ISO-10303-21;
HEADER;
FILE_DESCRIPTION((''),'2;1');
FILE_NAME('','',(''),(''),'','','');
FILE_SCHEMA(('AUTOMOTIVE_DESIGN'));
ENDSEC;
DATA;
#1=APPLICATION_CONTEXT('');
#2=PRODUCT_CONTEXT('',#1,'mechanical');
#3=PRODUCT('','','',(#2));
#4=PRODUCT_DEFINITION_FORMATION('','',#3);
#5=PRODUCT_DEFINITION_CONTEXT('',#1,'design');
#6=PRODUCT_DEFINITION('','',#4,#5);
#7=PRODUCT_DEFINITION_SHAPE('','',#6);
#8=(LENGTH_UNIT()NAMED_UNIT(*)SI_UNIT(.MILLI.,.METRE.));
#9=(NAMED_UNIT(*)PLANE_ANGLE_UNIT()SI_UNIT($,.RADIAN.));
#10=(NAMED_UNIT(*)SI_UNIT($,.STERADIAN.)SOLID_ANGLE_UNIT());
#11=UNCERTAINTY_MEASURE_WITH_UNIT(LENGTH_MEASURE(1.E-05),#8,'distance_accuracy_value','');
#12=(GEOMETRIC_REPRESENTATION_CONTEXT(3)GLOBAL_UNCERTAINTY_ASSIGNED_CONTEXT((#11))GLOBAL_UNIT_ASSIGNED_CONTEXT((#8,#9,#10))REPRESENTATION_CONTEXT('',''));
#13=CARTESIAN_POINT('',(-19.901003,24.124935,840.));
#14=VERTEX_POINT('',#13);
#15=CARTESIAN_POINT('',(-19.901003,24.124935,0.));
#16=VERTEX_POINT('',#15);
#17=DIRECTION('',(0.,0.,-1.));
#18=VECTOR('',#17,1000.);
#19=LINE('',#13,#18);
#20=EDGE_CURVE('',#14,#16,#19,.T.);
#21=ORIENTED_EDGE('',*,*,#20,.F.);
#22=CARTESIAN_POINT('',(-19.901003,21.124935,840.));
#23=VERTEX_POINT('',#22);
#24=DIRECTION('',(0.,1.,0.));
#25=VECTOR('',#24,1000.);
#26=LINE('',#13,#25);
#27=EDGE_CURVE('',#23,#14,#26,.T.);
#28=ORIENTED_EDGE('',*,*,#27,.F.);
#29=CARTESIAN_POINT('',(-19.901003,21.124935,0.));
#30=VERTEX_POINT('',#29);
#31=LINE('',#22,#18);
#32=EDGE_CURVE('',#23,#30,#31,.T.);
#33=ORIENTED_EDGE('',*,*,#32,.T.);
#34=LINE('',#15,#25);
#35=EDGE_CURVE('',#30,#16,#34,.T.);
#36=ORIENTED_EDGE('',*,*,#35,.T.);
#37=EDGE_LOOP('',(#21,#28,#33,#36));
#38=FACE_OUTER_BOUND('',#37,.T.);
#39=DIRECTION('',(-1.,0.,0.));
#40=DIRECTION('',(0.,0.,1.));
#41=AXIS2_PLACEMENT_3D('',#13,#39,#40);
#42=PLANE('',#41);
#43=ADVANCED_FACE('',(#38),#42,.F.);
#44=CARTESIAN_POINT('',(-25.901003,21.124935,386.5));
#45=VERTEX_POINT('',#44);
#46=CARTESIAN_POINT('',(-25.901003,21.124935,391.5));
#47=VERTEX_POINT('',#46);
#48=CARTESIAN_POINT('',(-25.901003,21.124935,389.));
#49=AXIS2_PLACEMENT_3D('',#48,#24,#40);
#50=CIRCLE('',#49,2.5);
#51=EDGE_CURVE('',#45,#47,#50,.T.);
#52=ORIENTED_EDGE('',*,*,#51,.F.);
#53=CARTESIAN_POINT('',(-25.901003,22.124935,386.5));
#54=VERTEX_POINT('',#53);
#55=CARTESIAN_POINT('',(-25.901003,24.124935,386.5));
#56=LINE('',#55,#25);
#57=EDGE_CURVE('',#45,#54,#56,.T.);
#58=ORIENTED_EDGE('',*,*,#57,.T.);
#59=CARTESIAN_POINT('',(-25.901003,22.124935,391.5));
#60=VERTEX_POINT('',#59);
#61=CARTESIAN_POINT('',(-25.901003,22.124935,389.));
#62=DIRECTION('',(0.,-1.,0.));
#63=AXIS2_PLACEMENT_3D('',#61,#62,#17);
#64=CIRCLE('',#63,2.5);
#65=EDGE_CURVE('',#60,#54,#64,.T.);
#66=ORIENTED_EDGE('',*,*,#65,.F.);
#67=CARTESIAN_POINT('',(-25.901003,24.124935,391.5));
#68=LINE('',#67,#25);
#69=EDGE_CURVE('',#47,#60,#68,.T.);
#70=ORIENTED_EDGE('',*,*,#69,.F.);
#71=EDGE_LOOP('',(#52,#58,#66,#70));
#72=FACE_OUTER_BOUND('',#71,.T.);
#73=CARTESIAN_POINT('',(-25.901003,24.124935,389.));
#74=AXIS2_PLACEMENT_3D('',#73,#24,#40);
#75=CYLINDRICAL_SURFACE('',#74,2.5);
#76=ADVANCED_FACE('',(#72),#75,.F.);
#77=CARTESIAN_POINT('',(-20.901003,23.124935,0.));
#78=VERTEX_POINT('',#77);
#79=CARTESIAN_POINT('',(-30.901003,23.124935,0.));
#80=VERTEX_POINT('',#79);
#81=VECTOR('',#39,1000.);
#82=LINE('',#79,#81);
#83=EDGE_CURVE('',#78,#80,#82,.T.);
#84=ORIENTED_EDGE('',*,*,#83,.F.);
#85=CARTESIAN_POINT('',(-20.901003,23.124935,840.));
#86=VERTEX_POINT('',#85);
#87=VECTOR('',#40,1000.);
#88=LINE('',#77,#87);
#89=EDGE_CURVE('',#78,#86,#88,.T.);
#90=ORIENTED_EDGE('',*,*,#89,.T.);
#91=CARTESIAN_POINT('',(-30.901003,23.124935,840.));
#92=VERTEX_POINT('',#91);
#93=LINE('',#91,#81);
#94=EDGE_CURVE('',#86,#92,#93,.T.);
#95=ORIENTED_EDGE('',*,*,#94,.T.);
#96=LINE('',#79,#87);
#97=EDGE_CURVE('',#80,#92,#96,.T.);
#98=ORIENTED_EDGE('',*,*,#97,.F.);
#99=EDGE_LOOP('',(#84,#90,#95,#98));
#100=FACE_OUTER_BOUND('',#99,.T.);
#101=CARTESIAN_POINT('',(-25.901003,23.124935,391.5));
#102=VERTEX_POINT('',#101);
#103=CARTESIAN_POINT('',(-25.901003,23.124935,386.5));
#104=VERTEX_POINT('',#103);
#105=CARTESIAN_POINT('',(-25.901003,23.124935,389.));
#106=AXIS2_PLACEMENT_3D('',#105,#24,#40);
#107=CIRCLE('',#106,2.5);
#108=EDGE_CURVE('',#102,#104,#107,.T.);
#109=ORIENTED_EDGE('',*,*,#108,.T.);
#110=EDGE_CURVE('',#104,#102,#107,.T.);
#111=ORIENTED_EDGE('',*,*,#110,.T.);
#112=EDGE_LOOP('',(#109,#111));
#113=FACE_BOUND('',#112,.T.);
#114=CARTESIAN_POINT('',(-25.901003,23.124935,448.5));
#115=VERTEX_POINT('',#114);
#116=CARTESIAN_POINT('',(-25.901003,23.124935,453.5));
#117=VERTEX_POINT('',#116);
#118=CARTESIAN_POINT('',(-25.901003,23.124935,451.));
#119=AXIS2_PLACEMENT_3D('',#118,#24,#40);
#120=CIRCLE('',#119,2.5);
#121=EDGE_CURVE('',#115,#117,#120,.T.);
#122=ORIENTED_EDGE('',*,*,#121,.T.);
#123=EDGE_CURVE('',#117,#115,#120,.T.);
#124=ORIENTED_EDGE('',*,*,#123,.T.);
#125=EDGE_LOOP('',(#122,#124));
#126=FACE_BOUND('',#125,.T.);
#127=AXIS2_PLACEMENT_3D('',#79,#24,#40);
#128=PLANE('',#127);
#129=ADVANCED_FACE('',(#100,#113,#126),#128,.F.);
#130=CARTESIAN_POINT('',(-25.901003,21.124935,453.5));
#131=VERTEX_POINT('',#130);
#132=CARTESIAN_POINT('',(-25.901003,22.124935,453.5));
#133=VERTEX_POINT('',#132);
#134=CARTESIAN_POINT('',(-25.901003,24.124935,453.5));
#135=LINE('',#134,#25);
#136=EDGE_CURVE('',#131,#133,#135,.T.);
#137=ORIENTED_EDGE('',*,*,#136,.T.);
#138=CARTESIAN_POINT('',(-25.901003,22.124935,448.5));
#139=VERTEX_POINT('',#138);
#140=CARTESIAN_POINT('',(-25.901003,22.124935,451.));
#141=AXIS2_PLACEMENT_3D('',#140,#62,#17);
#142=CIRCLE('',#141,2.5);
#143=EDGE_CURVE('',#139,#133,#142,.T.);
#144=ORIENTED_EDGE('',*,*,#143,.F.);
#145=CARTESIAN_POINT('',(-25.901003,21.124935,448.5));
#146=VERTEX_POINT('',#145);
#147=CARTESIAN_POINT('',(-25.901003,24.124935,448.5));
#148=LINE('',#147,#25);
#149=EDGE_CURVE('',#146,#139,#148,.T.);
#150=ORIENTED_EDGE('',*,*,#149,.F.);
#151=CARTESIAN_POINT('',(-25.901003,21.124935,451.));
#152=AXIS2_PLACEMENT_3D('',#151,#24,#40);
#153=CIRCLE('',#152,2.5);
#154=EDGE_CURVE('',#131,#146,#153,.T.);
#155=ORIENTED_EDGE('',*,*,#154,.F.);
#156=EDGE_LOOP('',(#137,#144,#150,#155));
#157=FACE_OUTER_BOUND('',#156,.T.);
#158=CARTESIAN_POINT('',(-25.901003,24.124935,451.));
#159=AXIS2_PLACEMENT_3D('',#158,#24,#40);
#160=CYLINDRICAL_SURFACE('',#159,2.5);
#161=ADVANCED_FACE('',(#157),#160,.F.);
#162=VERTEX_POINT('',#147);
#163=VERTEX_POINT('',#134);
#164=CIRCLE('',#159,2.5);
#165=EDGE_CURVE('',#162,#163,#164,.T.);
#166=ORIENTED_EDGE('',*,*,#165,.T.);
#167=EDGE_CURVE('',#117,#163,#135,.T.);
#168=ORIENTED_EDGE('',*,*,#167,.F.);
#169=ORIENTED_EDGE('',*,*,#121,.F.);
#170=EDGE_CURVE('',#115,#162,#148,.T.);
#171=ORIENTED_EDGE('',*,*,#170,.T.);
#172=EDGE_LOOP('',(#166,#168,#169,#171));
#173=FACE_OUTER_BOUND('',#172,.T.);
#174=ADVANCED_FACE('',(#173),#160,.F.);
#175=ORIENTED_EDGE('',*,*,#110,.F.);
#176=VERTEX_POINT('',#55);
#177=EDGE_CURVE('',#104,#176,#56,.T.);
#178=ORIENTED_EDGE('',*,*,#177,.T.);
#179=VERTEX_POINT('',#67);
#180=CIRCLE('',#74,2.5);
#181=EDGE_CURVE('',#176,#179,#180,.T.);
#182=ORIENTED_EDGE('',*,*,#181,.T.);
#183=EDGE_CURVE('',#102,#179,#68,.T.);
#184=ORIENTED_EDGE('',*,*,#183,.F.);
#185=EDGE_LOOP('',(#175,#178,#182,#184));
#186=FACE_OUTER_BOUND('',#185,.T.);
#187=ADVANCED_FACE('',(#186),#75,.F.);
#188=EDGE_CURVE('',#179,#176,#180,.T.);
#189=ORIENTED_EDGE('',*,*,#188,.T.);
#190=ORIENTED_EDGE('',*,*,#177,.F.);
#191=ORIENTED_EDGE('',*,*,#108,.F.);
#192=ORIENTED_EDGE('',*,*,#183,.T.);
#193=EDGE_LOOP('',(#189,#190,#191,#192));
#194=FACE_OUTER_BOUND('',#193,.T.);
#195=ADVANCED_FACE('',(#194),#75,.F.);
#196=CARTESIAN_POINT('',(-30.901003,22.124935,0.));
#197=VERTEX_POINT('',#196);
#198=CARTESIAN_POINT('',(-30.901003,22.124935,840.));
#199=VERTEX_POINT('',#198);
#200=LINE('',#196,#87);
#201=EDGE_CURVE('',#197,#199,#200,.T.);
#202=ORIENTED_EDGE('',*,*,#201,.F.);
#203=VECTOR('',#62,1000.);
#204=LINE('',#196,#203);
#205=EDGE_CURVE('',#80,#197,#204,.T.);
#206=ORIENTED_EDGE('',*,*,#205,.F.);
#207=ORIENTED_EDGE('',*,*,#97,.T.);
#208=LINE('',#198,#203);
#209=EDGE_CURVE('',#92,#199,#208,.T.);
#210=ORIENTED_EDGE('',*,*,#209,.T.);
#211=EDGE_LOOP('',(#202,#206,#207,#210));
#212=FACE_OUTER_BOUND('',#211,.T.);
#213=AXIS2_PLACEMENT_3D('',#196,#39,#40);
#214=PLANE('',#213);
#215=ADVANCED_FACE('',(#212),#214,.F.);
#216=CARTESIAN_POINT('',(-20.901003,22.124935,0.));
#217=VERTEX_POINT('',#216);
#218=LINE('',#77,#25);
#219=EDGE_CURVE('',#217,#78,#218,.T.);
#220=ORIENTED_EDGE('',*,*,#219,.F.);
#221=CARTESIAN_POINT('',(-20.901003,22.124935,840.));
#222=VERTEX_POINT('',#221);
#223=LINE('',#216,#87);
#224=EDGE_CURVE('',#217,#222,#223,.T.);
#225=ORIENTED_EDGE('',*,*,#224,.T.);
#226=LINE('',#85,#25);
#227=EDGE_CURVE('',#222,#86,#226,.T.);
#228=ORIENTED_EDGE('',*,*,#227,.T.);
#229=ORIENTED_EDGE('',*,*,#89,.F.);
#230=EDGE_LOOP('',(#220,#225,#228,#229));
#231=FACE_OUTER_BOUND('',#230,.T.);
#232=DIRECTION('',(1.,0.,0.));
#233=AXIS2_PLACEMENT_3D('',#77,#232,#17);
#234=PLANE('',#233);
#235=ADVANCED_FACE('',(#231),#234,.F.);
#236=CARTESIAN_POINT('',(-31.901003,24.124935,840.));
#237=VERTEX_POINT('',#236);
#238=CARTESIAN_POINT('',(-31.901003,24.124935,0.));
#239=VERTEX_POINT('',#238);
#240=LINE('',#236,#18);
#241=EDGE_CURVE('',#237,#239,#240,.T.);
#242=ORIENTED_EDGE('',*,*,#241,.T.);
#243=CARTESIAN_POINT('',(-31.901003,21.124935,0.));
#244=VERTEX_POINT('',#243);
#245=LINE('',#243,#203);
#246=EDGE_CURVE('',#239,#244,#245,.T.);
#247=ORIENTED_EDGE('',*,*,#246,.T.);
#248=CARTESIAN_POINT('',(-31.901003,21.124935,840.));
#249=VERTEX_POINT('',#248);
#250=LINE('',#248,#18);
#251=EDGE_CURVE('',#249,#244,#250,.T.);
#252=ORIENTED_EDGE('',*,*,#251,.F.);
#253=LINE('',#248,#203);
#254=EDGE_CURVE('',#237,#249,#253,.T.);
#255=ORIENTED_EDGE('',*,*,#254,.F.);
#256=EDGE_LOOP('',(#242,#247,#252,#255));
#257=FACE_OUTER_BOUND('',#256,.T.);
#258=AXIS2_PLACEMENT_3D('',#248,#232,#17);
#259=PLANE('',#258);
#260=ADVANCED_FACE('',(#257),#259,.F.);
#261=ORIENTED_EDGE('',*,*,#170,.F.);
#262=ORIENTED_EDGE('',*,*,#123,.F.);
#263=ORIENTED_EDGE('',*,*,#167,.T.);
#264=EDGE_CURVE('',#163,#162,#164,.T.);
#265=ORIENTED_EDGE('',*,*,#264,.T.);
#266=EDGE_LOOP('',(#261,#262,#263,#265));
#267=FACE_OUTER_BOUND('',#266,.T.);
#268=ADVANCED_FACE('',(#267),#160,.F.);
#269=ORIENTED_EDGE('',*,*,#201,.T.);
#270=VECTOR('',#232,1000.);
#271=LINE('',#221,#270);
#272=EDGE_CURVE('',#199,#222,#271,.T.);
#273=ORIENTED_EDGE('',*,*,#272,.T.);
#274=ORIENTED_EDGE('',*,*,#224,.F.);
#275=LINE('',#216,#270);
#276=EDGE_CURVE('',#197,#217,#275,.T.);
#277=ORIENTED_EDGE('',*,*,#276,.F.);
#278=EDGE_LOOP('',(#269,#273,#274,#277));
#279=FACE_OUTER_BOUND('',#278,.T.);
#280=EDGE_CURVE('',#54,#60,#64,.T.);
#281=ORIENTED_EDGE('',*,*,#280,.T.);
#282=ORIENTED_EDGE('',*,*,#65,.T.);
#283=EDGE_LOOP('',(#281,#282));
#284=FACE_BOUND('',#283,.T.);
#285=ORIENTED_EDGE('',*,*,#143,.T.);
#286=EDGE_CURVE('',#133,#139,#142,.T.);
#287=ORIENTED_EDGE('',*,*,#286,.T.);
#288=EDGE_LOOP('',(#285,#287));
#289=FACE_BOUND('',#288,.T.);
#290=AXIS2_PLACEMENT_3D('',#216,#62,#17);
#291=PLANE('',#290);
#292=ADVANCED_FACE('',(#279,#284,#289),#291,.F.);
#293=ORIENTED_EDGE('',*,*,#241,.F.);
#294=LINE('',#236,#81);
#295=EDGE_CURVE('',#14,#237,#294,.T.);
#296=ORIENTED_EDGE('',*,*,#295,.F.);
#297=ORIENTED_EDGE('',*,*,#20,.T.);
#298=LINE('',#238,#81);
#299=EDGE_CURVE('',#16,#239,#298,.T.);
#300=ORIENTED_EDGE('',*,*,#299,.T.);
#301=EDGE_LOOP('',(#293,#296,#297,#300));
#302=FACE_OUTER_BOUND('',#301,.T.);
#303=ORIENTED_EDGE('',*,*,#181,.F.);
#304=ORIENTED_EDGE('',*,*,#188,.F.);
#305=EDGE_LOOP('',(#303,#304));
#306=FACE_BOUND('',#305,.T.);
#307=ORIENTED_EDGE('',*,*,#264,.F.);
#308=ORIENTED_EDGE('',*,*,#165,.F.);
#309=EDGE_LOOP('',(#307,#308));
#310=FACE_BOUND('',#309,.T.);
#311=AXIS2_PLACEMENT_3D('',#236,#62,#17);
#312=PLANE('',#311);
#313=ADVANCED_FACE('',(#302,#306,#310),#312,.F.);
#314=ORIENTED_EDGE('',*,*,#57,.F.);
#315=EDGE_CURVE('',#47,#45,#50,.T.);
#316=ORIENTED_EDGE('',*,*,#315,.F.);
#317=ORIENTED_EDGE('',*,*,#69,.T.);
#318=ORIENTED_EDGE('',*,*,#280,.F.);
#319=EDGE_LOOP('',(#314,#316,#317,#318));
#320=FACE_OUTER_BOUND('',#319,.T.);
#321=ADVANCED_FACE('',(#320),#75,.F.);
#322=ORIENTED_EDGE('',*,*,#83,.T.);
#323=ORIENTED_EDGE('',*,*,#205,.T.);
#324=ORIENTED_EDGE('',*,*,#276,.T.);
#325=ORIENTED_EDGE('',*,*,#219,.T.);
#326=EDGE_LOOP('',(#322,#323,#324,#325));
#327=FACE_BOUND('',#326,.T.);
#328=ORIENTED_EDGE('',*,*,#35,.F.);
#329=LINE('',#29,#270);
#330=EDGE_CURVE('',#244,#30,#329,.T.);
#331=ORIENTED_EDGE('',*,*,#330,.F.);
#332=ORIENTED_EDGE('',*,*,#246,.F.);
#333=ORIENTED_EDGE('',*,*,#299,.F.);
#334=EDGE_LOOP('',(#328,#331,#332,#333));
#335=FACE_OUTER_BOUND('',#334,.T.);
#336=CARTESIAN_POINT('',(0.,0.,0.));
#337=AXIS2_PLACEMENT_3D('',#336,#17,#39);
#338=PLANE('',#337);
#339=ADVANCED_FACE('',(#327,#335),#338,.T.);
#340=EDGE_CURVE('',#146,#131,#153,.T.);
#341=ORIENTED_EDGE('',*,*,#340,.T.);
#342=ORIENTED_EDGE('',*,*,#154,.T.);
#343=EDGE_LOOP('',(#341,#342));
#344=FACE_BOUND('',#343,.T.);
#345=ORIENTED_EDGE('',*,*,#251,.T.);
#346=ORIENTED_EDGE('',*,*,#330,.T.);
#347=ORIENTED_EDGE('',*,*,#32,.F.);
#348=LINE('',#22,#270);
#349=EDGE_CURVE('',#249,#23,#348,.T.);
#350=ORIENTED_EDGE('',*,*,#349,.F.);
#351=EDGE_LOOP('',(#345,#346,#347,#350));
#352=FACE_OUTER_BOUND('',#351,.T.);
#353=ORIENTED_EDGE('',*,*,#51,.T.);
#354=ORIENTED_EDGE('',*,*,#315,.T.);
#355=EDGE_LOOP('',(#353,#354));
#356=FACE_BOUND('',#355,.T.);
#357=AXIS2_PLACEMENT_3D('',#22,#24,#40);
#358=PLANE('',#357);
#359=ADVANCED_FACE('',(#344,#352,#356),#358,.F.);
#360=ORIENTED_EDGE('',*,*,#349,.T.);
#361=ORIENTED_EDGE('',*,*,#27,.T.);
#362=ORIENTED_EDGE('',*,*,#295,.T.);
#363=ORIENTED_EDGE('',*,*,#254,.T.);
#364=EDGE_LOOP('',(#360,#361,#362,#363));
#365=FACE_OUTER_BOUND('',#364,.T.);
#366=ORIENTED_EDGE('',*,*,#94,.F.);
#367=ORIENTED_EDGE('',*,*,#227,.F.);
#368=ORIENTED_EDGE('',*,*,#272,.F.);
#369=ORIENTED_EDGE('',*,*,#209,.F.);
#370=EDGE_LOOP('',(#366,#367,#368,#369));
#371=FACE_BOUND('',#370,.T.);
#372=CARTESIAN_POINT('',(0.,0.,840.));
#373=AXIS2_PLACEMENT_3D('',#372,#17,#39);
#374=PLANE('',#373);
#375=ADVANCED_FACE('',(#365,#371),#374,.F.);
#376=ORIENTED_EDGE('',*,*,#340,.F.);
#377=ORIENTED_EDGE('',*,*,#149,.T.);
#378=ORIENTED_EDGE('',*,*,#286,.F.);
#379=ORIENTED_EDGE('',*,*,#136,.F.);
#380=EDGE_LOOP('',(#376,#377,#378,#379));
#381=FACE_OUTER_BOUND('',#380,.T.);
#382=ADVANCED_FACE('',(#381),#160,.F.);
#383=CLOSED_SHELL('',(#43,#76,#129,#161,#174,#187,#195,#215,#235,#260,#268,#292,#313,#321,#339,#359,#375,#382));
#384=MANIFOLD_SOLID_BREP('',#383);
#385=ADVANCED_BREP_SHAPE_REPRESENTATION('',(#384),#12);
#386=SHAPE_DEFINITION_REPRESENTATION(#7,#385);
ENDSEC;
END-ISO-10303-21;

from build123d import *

# Parameters (mm, degrees)
SKETCH1_W             = 12
SKETCH1_H             = 3
BOSS_EXTRUDE1_DEPTH   = 840
SKETCH2_W             = 10
SKETCH2_H             = 1
CUT_EXTRUDE1_DEPTH    = 841.951655259
M6_TAPPED_HOLE1_D     = 5
M6_TAPPED_HOLE1_DEPTH = 15
M6_TAPPED_HOLE1_TIP   = 1.502151548


with BuildPart() as part:
    # Sketch1 → Boss-Extrude1 (new body)
    with BuildSketch(Plane.XY):
        with Locations((-25.901003365, 22.624934563)):
            Rectangle(SKETCH1_W, SKETCH1_H)
    extrude(amount=BOSS_EXTRUDE1_DEPTH)

    # Sketch2 → Cut-Extrude1 (cut, through all)
    with BuildSketch(Plane.XY.offset(840)):
        with Locations((-25.901003365, 22.624934563)):
            Rectangle(SKETCH2_W, SKETCH2_H)
    extrude(amount=-CUT_EXTRUDE1_DEPTH, mode=Mode.SUBTRACT)

    # M6 Tapped Hole1
    with Locations(Plane(origin=(-25.901003365, 24.124934563, 389), x_dir=(0, 0, 1), z_dir=(0, 1, 0))):
        with Locations((0, 0), (62, 0)):
            Hole(M6_TAPPED_HOLE1_D / 2, depth=M6_TAPPED_HOLE1_DEPTH)
            with Locations((0, 0, -(M6_TAPPED_HOLE1_DEPTH + M6_TAPPED_HOLE1_TIP / 2))):  # 118° drill point
                Cone(0, M6_TAPPED_HOLE1_D / 2, M6_TAPPED_HOLE1_TIP, mode=Mode.SUBTRACT)


solid = part.part
